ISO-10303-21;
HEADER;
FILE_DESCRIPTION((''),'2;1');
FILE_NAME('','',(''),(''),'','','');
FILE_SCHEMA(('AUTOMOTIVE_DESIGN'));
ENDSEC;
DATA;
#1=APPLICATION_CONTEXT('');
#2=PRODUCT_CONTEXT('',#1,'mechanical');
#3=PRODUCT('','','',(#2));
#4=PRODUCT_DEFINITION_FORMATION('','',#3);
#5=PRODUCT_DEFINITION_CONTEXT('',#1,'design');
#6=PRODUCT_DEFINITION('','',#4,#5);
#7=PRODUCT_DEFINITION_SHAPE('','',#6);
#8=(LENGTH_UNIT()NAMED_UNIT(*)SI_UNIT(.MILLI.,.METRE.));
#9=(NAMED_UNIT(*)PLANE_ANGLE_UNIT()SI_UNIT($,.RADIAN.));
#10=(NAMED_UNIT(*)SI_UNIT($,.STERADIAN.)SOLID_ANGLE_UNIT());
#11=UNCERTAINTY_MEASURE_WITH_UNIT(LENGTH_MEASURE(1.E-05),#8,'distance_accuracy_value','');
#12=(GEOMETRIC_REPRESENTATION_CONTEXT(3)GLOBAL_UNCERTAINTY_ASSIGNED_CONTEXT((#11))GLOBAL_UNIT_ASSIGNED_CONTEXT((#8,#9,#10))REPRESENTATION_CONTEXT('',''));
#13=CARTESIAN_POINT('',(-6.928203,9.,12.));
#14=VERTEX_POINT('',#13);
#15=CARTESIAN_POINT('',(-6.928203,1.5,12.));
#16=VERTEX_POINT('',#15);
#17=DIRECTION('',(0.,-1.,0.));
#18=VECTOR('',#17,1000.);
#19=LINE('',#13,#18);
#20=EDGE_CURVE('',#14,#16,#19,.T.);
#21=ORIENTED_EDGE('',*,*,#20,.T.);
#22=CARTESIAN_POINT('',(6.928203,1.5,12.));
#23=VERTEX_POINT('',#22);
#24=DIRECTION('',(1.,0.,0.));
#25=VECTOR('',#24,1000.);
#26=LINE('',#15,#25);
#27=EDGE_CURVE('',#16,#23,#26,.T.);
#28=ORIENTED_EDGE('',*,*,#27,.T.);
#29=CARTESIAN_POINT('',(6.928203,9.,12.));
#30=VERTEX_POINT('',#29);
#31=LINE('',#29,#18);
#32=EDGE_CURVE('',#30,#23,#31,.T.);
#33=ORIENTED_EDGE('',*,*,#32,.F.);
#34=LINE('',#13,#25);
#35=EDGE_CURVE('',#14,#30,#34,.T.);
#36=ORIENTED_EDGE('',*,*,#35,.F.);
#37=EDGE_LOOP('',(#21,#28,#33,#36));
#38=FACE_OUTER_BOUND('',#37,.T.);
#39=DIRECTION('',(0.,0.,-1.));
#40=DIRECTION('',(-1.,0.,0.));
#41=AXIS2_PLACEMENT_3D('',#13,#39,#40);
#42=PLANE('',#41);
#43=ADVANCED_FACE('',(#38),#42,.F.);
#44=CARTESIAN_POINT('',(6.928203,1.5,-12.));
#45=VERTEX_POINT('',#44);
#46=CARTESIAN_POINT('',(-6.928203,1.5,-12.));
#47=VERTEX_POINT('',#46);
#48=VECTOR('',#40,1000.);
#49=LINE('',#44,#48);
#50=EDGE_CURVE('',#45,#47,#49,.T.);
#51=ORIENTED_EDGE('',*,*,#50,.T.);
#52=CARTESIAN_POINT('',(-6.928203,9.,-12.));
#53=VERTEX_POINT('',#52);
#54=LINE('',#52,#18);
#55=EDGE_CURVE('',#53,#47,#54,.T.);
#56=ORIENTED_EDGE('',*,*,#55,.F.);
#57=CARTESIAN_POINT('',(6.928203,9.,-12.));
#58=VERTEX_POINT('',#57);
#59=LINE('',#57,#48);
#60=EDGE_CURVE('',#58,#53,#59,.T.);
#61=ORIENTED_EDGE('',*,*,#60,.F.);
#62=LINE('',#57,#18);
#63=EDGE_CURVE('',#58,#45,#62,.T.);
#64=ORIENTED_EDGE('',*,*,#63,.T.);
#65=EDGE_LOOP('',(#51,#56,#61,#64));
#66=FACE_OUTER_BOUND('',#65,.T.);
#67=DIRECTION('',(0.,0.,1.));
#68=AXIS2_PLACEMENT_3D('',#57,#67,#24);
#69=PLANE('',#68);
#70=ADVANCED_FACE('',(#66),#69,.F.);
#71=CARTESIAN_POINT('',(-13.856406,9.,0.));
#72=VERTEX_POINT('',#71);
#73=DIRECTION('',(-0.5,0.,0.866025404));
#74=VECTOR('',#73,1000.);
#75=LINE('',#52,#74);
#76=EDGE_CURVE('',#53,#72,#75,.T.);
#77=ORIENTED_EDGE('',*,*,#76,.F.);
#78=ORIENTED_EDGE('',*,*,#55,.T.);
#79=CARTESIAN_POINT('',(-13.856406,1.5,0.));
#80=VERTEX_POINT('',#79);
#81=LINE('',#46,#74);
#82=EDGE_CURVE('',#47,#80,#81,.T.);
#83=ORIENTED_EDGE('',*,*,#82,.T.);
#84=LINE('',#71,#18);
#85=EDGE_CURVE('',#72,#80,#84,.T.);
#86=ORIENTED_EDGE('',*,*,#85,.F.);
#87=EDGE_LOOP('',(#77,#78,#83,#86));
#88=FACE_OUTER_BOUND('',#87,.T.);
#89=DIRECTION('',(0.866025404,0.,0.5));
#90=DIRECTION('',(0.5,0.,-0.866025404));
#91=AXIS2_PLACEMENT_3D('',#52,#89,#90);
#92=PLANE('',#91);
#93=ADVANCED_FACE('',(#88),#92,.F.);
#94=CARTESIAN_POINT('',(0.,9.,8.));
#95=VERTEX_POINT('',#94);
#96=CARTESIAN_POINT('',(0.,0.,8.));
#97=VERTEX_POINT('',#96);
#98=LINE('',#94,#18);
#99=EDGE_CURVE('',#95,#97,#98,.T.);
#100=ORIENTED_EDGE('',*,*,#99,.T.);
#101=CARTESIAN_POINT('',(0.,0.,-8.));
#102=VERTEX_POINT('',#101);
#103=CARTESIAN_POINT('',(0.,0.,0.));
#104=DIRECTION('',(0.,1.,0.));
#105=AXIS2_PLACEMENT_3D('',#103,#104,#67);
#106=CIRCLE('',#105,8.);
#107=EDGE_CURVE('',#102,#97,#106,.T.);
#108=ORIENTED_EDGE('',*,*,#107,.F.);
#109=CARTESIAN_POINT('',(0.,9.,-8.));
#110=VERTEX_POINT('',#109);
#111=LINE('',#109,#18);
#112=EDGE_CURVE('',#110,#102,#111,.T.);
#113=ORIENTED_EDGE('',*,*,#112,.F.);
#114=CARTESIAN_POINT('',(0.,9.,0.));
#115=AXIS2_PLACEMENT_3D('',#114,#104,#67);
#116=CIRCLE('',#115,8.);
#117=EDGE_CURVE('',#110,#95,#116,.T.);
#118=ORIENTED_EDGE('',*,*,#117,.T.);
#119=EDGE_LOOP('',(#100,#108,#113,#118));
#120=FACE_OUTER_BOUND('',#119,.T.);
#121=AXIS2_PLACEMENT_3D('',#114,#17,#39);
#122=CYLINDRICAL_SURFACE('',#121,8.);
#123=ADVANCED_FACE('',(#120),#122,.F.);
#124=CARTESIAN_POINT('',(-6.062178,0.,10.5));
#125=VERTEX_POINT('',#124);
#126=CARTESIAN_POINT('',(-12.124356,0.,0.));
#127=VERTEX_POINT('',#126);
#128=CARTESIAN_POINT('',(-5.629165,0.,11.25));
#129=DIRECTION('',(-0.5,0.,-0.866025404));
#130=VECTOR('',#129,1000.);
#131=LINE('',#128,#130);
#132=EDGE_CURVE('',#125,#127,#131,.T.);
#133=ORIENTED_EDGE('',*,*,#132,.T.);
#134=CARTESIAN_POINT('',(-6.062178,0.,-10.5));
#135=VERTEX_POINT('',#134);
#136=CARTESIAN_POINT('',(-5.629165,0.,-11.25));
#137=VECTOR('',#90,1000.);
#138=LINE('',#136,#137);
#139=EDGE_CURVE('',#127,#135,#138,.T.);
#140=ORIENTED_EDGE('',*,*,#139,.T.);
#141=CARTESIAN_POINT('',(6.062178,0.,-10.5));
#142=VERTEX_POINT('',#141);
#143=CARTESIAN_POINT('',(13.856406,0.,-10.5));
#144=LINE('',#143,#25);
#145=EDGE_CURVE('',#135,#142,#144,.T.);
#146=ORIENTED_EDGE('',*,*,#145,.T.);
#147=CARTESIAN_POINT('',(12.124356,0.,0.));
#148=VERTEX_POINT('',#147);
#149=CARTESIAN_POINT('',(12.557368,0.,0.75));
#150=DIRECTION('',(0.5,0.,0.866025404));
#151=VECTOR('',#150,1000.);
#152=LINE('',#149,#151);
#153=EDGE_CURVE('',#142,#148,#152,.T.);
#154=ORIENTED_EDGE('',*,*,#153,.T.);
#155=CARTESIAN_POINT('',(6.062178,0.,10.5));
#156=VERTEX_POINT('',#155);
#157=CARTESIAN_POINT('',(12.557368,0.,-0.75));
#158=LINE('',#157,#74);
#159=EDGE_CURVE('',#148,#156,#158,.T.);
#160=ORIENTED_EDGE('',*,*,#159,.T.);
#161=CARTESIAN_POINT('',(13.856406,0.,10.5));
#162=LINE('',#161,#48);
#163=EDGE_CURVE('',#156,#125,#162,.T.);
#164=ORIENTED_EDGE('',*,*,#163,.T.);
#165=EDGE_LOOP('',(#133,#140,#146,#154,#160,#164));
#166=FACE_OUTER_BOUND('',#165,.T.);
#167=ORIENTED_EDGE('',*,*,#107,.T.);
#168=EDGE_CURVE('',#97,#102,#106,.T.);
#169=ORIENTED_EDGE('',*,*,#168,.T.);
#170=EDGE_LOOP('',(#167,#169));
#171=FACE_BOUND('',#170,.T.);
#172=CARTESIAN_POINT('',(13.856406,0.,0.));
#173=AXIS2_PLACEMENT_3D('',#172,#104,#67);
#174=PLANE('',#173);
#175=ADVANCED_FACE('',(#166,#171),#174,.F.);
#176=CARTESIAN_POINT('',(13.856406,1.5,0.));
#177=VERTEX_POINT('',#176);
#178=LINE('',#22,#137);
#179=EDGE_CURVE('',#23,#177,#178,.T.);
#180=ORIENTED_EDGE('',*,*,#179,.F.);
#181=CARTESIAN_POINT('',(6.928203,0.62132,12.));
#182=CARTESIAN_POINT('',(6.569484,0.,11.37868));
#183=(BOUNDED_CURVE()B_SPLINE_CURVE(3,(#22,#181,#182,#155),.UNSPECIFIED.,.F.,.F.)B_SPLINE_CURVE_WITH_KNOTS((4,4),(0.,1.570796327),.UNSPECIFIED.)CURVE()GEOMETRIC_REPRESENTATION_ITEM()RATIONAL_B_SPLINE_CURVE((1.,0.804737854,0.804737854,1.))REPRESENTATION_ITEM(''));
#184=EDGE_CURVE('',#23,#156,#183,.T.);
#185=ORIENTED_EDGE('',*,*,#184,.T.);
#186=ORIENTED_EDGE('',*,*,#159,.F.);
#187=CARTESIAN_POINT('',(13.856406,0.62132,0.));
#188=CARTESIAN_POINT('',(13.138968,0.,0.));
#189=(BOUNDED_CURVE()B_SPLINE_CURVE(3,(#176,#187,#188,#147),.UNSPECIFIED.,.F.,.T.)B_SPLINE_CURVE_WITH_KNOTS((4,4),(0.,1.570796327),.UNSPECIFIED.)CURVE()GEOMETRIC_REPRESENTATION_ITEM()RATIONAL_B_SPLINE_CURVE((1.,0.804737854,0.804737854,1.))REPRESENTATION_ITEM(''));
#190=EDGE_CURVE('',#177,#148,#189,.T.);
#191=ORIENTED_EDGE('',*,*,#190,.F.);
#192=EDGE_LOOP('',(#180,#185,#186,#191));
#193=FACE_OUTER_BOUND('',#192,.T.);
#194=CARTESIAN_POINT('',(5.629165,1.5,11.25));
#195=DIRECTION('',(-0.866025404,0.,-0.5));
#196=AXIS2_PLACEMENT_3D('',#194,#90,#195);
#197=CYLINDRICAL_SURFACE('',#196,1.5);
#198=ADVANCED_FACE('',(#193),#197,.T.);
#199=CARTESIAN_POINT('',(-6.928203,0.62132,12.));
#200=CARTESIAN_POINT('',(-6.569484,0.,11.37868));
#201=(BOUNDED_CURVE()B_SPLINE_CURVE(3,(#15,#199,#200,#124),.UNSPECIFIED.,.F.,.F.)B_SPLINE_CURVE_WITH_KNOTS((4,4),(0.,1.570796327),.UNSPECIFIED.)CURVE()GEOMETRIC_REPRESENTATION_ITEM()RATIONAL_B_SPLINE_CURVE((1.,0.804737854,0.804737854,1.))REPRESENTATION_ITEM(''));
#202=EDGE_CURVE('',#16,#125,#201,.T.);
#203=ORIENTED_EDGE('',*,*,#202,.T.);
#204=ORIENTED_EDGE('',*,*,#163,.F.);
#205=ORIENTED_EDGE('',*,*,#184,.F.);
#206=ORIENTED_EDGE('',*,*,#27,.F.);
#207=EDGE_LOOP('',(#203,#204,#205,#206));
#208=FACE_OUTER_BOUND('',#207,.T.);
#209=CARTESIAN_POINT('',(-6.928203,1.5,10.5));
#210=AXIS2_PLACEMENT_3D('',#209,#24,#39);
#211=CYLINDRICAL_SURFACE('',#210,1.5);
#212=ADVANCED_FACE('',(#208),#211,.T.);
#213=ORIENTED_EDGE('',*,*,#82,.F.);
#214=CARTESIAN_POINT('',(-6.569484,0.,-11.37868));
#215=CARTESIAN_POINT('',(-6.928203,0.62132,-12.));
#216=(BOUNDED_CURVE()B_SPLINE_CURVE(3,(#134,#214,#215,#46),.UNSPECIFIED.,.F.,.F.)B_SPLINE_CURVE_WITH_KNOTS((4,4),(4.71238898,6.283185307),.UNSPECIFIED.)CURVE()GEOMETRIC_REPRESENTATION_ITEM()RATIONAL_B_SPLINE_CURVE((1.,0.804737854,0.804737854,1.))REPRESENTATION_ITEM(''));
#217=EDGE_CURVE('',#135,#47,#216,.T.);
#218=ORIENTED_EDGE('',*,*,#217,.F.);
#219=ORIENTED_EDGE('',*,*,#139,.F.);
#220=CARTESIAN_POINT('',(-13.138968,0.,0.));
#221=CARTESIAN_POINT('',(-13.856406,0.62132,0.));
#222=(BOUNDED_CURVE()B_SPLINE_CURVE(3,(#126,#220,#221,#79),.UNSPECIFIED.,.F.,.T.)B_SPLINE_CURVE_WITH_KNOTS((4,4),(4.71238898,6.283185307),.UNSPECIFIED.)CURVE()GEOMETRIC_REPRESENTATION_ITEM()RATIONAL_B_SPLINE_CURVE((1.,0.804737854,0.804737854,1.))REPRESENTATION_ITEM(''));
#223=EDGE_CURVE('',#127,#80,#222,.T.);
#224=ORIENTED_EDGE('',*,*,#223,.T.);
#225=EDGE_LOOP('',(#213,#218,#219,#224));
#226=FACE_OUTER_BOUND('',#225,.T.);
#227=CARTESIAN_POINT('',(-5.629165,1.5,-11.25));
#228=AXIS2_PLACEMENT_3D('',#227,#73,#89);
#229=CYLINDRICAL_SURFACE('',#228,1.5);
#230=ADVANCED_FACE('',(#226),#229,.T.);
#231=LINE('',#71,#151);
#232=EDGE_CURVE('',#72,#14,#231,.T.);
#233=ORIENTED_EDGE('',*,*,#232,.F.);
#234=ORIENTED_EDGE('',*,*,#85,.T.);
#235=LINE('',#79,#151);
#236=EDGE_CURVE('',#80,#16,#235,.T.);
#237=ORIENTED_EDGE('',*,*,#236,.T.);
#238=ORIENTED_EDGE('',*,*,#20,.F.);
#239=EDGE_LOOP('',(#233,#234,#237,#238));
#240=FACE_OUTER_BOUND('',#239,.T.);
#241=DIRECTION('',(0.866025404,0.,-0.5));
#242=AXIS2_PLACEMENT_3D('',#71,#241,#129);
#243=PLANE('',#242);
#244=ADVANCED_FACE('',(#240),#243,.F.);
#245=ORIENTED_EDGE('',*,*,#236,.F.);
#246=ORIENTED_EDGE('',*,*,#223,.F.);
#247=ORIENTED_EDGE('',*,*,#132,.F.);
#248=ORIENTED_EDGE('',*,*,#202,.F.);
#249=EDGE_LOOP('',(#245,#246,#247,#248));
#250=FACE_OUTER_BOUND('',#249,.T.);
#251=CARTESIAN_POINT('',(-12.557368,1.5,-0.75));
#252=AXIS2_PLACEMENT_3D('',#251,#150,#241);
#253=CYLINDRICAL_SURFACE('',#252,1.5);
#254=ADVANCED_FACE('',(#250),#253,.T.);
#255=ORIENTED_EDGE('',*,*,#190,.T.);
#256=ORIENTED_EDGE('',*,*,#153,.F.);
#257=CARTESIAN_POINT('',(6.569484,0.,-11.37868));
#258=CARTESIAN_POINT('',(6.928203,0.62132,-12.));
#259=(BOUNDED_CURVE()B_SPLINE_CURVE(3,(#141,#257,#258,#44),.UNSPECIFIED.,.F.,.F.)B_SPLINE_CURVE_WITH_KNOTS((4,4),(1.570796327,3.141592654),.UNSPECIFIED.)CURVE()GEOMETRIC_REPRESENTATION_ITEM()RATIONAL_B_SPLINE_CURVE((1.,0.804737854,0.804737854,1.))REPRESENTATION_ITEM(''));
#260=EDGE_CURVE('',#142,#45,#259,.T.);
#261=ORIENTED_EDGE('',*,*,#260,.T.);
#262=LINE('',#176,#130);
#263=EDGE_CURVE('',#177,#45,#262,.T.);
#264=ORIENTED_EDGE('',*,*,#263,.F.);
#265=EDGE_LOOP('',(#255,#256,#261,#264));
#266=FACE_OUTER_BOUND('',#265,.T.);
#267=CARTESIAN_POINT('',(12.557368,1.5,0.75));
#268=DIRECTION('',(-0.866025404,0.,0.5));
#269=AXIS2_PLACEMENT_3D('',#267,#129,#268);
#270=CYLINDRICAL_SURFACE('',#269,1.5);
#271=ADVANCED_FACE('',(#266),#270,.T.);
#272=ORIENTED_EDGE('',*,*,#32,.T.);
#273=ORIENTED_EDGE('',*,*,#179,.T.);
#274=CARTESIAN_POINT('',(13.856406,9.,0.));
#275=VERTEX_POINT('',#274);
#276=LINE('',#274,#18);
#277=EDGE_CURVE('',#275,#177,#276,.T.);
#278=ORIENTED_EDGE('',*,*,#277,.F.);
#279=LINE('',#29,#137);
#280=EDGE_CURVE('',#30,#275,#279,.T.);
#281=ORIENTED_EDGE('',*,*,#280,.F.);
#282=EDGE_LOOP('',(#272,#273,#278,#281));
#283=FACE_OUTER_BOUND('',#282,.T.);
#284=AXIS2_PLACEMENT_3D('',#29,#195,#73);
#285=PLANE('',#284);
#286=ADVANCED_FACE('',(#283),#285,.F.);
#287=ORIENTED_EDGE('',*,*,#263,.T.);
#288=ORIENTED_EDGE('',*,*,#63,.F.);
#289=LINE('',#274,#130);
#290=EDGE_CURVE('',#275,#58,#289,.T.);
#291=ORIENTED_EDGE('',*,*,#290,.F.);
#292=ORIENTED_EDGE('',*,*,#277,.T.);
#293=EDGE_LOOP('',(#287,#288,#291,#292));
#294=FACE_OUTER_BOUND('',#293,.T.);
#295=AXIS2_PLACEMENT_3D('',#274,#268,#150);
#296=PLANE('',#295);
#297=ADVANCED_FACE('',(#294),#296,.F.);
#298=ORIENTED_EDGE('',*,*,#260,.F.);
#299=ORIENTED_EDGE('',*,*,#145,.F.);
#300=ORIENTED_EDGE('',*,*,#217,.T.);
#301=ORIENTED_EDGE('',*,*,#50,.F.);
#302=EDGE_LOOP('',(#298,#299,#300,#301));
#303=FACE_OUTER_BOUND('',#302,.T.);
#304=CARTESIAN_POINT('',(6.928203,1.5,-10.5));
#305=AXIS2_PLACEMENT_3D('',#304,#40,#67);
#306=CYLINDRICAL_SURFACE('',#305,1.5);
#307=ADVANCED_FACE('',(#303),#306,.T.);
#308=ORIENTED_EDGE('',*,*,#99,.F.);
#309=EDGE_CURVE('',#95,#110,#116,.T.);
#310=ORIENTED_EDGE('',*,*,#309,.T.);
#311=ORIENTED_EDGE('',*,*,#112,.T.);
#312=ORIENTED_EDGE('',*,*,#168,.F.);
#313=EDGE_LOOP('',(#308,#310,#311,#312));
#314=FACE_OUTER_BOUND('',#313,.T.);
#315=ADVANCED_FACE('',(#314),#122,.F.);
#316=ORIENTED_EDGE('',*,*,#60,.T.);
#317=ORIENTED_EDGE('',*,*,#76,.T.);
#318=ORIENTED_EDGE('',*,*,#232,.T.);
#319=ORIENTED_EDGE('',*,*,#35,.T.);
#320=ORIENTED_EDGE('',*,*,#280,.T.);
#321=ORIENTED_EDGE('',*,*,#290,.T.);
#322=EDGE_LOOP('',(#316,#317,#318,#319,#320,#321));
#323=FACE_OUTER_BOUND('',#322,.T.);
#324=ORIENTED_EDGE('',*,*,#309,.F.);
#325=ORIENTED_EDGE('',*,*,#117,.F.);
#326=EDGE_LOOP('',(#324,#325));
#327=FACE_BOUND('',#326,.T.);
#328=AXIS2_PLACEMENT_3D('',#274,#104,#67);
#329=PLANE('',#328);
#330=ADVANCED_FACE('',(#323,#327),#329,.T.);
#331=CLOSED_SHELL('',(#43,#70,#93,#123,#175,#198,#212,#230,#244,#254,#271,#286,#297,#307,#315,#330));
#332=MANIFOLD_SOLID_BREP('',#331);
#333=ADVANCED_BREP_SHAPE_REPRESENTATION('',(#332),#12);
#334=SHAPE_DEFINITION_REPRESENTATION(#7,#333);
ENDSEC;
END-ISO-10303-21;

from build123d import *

# Parameters (mm, degrees)
SKETCH1_R      = 8
EXTRUDE1_DEPTH = 9
FILLET1_R      = 1.5


with BuildPart() as part:
    # Sketch1 → Extrude1 (new body)
    with BuildSketch(Plane(origin=(0, 0, 0), x_dir=(1, 0, 0), z_dir=(0, 1, 0))):
        Polygon((13.856406461, 0), (6.92820323, 12), (-6.92820323, 12), (-13.856406461, 0), (-6.92820323, -12), (6.92820323, -12), align=None)
        with Locations(Location((0, 0, 0), (0, 0, 270))):
            Circle(SKETCH1_R, mode=Mode.SUBTRACT)
    extrude(amount=EXTRUDE1_DEPTH)

    # Fillet1
    fillet1_edges = [part.edges().sort_by_distance(p)[0] for p in [
        (0, 0, 12),
        (-10.392304845, 0, 6),
        (-10.392304845, 0, -6),
        (0, 0, -12),
        (10.392304845, 0, -6),
        (10.392304845, 0, 6),
    ]]
    fillet(fillet1_edges, radius=FILLET1_R)


solid = part.part
